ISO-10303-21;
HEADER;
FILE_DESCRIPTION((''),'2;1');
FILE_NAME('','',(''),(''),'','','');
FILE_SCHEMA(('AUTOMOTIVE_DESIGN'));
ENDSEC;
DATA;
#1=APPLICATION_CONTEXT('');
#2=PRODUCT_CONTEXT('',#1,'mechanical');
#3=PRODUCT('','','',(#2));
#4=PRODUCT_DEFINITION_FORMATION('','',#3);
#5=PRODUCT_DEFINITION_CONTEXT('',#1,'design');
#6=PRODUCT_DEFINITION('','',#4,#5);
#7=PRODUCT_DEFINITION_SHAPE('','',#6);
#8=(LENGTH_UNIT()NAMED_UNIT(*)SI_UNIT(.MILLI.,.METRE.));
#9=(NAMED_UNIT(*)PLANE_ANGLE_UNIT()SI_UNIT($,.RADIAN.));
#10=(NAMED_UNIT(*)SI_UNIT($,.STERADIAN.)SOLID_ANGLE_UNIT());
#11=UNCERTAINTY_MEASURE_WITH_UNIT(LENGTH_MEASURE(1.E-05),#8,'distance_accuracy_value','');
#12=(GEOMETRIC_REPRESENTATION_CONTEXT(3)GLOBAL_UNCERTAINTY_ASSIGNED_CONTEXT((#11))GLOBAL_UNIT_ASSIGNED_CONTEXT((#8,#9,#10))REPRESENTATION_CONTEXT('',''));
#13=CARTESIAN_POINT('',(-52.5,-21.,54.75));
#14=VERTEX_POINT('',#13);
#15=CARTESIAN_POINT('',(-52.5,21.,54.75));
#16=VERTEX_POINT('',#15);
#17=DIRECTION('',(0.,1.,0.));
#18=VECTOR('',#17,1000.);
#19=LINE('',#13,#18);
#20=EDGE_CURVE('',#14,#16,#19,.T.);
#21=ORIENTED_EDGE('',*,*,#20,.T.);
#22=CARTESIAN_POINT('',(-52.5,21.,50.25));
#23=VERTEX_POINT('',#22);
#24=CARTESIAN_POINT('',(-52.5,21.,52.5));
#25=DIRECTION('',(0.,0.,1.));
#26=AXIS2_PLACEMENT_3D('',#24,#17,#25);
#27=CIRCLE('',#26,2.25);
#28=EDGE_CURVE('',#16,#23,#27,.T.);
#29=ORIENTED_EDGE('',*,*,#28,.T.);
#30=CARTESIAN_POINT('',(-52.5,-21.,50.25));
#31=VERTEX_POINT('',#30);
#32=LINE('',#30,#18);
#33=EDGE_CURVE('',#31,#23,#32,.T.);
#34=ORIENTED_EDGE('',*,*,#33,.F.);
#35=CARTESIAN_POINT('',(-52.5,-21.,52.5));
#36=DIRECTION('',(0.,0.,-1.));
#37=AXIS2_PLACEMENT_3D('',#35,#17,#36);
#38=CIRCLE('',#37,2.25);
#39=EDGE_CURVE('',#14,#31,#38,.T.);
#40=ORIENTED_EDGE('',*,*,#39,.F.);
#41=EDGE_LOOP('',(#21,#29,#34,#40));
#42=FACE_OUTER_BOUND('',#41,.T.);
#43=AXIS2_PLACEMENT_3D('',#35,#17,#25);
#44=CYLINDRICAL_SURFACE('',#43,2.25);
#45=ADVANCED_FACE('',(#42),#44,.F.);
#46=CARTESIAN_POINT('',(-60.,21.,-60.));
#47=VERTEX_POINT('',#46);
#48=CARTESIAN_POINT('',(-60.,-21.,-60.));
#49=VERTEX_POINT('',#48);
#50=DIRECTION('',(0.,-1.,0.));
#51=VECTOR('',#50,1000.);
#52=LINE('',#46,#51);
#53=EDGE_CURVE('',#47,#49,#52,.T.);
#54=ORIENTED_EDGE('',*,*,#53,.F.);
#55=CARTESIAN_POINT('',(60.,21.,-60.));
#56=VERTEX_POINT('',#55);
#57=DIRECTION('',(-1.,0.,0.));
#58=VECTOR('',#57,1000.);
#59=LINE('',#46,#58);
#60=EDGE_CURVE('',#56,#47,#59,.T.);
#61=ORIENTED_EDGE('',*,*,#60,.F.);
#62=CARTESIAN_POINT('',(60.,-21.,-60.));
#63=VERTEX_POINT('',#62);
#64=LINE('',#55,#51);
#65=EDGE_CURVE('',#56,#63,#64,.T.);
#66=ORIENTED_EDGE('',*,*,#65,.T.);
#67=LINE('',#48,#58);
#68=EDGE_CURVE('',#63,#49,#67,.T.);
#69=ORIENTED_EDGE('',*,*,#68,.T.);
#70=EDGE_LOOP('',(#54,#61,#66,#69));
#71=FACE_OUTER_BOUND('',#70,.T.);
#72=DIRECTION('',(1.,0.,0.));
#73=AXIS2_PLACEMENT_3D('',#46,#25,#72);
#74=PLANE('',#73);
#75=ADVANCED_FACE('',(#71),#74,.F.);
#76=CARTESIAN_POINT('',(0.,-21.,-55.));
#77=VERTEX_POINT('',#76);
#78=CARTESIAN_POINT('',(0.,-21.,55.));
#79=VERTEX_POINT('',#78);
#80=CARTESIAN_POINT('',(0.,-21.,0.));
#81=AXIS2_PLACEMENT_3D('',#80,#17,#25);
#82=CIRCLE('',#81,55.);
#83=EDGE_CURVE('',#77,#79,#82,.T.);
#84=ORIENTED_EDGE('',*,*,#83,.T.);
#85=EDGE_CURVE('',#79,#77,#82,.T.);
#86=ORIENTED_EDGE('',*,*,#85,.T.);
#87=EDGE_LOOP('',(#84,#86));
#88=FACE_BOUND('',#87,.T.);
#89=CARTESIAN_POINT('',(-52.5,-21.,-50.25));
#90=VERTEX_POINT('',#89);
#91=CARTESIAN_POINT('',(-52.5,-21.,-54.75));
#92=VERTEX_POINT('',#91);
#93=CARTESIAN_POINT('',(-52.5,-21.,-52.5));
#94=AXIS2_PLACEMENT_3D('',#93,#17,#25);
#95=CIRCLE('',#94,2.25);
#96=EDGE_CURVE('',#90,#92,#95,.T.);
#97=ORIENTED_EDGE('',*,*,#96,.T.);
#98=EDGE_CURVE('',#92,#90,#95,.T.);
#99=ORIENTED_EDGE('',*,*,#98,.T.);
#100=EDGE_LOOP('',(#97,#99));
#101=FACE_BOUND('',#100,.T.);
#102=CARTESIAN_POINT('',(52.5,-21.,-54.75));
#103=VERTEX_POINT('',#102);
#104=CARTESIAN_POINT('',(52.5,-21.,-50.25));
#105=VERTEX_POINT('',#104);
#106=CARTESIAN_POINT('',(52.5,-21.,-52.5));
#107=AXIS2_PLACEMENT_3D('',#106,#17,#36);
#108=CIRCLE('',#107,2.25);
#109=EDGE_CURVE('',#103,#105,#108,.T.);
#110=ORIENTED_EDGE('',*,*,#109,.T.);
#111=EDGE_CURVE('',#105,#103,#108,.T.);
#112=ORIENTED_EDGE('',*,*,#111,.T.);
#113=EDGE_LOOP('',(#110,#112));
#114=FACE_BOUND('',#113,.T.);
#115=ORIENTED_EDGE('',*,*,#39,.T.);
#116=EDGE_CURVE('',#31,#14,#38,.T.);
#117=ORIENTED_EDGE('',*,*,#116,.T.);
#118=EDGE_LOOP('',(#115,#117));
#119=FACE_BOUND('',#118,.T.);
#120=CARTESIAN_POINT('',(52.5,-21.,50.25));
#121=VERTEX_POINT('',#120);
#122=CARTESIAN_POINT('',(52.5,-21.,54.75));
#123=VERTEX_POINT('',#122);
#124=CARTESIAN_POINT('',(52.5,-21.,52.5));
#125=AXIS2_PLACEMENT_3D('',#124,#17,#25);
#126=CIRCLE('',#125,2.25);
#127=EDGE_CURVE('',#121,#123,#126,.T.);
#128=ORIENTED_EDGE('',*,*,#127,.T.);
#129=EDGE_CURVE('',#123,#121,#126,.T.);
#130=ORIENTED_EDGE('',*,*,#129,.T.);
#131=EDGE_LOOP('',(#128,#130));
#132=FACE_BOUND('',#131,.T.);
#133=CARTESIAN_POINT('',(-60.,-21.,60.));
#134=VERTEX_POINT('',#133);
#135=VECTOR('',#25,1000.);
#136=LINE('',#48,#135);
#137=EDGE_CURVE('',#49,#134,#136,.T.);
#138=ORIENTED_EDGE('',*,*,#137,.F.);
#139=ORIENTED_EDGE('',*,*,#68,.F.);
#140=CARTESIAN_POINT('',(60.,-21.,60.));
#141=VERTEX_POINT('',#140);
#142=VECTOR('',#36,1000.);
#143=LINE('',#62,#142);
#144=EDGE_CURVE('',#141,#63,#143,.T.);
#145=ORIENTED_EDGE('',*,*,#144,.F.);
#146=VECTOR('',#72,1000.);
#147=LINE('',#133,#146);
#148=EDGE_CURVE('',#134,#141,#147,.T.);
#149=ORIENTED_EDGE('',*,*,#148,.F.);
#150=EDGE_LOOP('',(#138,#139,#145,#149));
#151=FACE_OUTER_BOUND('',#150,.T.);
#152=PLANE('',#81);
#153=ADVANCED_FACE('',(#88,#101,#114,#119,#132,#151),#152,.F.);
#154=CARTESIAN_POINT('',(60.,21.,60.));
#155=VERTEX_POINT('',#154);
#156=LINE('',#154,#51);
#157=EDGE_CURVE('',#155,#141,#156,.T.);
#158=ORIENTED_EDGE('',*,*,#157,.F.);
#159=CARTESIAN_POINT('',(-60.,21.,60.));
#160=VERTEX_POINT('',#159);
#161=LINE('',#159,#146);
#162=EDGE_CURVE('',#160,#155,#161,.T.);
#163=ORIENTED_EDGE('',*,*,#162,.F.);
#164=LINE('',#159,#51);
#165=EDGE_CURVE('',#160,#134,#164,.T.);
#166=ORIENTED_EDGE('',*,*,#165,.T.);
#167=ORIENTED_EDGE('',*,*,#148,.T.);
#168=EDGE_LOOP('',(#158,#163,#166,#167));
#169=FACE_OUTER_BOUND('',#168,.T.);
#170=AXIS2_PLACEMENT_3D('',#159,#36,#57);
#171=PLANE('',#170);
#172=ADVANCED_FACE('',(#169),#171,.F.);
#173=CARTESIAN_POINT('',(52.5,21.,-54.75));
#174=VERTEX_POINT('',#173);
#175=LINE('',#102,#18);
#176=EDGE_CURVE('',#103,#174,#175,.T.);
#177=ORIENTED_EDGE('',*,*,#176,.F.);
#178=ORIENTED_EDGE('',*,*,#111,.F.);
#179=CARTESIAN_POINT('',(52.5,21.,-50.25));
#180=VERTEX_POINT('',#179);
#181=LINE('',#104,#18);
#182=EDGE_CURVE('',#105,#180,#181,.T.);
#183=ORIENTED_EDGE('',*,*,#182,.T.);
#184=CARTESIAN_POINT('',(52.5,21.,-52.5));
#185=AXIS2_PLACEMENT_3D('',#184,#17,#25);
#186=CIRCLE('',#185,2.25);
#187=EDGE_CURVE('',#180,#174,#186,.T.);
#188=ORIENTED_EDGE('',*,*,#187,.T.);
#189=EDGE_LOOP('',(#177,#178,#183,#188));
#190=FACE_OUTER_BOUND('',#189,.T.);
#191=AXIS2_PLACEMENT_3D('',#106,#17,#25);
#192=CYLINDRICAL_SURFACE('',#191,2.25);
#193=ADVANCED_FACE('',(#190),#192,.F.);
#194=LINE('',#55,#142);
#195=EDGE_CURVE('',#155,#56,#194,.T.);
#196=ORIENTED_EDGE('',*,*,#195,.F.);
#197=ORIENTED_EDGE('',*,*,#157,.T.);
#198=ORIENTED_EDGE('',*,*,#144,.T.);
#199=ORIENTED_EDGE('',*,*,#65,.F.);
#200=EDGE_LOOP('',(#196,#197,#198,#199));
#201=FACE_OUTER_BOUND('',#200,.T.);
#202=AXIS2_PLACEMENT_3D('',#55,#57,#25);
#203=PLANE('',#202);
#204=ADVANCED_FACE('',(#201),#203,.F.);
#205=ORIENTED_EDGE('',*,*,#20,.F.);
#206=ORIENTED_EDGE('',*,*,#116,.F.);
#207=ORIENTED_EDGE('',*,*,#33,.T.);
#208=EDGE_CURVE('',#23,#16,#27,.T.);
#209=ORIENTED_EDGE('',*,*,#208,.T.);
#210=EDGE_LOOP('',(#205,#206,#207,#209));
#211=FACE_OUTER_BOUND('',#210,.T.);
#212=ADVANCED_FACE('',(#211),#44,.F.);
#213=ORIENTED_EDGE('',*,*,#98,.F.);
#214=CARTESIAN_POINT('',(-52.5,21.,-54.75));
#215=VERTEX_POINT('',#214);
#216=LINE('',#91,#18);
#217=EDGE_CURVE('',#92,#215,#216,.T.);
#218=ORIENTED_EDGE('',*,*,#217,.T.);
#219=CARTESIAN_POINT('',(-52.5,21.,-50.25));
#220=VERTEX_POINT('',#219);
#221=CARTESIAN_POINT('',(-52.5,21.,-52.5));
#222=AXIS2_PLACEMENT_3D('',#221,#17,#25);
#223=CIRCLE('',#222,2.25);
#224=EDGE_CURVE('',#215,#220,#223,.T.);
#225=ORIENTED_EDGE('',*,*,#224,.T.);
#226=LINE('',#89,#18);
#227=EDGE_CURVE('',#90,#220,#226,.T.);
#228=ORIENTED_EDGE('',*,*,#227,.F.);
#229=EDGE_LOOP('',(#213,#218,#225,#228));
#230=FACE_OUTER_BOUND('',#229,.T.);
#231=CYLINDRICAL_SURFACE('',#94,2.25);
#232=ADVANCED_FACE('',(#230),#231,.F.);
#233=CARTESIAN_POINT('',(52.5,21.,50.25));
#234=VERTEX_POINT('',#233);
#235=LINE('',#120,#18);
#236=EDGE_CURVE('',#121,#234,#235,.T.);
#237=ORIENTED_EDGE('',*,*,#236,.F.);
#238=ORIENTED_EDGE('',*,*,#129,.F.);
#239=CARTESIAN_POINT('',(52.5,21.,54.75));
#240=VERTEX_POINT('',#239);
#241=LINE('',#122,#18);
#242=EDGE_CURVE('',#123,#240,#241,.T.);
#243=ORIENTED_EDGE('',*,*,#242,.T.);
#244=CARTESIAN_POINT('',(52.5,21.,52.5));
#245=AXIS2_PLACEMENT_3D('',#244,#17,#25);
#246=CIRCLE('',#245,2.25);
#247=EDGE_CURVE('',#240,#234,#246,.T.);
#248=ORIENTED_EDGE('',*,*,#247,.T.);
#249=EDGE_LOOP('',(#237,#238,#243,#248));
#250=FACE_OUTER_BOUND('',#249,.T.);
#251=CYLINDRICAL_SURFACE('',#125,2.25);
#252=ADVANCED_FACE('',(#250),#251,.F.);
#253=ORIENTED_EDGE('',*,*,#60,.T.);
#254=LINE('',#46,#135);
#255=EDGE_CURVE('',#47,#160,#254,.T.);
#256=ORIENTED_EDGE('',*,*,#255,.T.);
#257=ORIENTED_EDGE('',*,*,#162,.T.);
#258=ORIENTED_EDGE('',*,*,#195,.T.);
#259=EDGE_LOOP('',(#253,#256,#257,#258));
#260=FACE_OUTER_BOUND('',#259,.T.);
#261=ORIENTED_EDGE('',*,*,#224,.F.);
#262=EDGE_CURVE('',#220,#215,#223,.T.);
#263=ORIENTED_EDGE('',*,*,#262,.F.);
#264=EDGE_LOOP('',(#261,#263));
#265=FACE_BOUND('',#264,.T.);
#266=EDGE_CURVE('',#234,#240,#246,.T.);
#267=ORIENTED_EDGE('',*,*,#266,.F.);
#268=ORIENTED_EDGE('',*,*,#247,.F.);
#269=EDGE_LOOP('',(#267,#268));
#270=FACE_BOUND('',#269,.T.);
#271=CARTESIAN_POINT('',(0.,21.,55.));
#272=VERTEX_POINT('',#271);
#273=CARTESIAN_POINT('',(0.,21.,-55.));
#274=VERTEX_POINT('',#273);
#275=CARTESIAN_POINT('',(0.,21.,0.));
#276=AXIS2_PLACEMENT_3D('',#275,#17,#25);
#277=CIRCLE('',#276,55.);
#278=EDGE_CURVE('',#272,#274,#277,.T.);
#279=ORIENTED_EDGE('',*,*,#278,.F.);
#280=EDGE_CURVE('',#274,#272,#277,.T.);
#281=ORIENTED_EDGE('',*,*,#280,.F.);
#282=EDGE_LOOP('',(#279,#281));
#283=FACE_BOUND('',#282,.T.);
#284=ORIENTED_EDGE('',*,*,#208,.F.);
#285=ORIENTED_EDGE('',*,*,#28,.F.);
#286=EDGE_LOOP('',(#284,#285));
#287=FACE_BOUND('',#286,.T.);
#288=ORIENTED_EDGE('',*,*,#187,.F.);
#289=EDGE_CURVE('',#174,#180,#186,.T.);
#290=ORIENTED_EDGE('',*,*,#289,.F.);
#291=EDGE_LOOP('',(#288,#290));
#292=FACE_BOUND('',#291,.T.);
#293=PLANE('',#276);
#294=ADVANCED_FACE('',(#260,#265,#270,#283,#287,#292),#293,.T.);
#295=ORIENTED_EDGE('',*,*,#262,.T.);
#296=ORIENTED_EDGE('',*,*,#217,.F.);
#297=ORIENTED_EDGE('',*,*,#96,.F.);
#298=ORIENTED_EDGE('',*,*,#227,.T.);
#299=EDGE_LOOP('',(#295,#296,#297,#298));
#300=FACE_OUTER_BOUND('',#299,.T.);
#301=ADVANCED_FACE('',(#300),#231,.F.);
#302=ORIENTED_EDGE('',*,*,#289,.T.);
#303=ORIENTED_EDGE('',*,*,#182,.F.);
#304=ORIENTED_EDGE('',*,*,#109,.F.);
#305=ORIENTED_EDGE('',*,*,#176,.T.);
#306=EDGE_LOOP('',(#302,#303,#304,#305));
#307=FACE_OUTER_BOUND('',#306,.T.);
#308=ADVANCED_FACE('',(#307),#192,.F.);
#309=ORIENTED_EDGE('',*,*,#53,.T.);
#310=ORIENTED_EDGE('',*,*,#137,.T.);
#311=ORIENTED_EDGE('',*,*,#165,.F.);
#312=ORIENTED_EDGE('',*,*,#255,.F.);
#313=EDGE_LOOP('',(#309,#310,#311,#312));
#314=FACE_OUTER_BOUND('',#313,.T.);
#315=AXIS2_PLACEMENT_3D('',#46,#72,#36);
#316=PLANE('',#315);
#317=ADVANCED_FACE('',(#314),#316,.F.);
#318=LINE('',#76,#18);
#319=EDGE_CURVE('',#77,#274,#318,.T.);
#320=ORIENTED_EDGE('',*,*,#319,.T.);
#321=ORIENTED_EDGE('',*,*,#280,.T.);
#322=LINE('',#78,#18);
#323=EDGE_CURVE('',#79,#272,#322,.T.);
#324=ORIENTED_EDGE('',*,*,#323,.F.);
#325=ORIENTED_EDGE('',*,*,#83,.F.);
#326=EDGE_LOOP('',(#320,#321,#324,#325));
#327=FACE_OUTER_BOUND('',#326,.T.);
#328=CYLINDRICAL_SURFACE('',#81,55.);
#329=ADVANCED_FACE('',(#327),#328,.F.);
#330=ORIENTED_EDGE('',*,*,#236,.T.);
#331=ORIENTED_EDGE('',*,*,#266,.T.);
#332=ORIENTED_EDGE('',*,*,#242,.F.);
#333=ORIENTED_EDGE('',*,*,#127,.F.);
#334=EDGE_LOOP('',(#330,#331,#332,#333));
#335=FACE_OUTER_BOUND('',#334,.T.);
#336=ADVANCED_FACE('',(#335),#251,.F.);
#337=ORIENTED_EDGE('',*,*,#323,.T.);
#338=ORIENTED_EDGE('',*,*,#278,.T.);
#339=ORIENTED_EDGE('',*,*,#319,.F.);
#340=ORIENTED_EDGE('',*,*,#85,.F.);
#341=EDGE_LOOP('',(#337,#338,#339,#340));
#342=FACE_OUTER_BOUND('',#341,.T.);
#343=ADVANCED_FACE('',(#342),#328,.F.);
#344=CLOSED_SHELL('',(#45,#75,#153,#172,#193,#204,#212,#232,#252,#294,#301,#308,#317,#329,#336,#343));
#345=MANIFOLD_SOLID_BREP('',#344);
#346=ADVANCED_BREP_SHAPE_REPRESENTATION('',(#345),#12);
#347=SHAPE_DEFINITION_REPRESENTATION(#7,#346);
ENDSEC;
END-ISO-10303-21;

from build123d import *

# Parameters (mm, degrees)
SKETCH_1_W               = 120
SKETCH_1_H               = 120
EXTRUDE_1_DEPTH          = 21
CUT_EXTRUDE_1_DEPTH      = 95.678403028
CUT_EXTRUDE_1_DEPTH_BACK = 95.678403028
SKETCH_2_R               = 55
SKETCH_2_R_2             = 2.25


with BuildPart() as part:
    # 草图1 → 凸台-拉伸1 (new, symmetric)
    with BuildSketch(Plane(origin=(0, 0, 0), x_dir=(1, 0, 0), z_dir=(0, 1, 0))):
        Rectangle(SKETCH_1_W, SKETCH_1_H)
    extrude(amount=EXTRUDE_1_DEPTH, both=True)

    # 草图2 → 切除-拉伸1 (cut, two sides: drawn at the far end of the back side and taken through both)
    with BuildSketch(Plane(origin=(0, 21, 0), x_dir=(1, 0, 0), z_dir=(0, 1, 0)).offset(-CUT_EXTRUDE_1_DEPTH_BACK)):
        with Locations(Location((0, 0, 0), (0, 0, 270))):
            Circle(SKETCH_2_R)
        with Locations(Location((-52.5, 52.5, 0), (0, 0, 270))):
            Circle(SKETCH_2_R_2)
        with Locations(Location((52.5, 52.5, 0), (0, 0, 270))):
            Circle(SKETCH_2_R_2)
        with Locations(Location((52.5, -52.5, 0), (0, 0, 270))):
            Circle(SKETCH_2_R_2)
        with Locations(Location((-52.5, -52.5, 0), (0, 0, 270))):
            Circle(SKETCH_2_R_2)
    extrude(amount=CUT_EXTRUDE_1_DEPTH + CUT_EXTRUDE_1_DEPTH_BACK, mode=Mode.SUBTRACT)


solid = part.part
